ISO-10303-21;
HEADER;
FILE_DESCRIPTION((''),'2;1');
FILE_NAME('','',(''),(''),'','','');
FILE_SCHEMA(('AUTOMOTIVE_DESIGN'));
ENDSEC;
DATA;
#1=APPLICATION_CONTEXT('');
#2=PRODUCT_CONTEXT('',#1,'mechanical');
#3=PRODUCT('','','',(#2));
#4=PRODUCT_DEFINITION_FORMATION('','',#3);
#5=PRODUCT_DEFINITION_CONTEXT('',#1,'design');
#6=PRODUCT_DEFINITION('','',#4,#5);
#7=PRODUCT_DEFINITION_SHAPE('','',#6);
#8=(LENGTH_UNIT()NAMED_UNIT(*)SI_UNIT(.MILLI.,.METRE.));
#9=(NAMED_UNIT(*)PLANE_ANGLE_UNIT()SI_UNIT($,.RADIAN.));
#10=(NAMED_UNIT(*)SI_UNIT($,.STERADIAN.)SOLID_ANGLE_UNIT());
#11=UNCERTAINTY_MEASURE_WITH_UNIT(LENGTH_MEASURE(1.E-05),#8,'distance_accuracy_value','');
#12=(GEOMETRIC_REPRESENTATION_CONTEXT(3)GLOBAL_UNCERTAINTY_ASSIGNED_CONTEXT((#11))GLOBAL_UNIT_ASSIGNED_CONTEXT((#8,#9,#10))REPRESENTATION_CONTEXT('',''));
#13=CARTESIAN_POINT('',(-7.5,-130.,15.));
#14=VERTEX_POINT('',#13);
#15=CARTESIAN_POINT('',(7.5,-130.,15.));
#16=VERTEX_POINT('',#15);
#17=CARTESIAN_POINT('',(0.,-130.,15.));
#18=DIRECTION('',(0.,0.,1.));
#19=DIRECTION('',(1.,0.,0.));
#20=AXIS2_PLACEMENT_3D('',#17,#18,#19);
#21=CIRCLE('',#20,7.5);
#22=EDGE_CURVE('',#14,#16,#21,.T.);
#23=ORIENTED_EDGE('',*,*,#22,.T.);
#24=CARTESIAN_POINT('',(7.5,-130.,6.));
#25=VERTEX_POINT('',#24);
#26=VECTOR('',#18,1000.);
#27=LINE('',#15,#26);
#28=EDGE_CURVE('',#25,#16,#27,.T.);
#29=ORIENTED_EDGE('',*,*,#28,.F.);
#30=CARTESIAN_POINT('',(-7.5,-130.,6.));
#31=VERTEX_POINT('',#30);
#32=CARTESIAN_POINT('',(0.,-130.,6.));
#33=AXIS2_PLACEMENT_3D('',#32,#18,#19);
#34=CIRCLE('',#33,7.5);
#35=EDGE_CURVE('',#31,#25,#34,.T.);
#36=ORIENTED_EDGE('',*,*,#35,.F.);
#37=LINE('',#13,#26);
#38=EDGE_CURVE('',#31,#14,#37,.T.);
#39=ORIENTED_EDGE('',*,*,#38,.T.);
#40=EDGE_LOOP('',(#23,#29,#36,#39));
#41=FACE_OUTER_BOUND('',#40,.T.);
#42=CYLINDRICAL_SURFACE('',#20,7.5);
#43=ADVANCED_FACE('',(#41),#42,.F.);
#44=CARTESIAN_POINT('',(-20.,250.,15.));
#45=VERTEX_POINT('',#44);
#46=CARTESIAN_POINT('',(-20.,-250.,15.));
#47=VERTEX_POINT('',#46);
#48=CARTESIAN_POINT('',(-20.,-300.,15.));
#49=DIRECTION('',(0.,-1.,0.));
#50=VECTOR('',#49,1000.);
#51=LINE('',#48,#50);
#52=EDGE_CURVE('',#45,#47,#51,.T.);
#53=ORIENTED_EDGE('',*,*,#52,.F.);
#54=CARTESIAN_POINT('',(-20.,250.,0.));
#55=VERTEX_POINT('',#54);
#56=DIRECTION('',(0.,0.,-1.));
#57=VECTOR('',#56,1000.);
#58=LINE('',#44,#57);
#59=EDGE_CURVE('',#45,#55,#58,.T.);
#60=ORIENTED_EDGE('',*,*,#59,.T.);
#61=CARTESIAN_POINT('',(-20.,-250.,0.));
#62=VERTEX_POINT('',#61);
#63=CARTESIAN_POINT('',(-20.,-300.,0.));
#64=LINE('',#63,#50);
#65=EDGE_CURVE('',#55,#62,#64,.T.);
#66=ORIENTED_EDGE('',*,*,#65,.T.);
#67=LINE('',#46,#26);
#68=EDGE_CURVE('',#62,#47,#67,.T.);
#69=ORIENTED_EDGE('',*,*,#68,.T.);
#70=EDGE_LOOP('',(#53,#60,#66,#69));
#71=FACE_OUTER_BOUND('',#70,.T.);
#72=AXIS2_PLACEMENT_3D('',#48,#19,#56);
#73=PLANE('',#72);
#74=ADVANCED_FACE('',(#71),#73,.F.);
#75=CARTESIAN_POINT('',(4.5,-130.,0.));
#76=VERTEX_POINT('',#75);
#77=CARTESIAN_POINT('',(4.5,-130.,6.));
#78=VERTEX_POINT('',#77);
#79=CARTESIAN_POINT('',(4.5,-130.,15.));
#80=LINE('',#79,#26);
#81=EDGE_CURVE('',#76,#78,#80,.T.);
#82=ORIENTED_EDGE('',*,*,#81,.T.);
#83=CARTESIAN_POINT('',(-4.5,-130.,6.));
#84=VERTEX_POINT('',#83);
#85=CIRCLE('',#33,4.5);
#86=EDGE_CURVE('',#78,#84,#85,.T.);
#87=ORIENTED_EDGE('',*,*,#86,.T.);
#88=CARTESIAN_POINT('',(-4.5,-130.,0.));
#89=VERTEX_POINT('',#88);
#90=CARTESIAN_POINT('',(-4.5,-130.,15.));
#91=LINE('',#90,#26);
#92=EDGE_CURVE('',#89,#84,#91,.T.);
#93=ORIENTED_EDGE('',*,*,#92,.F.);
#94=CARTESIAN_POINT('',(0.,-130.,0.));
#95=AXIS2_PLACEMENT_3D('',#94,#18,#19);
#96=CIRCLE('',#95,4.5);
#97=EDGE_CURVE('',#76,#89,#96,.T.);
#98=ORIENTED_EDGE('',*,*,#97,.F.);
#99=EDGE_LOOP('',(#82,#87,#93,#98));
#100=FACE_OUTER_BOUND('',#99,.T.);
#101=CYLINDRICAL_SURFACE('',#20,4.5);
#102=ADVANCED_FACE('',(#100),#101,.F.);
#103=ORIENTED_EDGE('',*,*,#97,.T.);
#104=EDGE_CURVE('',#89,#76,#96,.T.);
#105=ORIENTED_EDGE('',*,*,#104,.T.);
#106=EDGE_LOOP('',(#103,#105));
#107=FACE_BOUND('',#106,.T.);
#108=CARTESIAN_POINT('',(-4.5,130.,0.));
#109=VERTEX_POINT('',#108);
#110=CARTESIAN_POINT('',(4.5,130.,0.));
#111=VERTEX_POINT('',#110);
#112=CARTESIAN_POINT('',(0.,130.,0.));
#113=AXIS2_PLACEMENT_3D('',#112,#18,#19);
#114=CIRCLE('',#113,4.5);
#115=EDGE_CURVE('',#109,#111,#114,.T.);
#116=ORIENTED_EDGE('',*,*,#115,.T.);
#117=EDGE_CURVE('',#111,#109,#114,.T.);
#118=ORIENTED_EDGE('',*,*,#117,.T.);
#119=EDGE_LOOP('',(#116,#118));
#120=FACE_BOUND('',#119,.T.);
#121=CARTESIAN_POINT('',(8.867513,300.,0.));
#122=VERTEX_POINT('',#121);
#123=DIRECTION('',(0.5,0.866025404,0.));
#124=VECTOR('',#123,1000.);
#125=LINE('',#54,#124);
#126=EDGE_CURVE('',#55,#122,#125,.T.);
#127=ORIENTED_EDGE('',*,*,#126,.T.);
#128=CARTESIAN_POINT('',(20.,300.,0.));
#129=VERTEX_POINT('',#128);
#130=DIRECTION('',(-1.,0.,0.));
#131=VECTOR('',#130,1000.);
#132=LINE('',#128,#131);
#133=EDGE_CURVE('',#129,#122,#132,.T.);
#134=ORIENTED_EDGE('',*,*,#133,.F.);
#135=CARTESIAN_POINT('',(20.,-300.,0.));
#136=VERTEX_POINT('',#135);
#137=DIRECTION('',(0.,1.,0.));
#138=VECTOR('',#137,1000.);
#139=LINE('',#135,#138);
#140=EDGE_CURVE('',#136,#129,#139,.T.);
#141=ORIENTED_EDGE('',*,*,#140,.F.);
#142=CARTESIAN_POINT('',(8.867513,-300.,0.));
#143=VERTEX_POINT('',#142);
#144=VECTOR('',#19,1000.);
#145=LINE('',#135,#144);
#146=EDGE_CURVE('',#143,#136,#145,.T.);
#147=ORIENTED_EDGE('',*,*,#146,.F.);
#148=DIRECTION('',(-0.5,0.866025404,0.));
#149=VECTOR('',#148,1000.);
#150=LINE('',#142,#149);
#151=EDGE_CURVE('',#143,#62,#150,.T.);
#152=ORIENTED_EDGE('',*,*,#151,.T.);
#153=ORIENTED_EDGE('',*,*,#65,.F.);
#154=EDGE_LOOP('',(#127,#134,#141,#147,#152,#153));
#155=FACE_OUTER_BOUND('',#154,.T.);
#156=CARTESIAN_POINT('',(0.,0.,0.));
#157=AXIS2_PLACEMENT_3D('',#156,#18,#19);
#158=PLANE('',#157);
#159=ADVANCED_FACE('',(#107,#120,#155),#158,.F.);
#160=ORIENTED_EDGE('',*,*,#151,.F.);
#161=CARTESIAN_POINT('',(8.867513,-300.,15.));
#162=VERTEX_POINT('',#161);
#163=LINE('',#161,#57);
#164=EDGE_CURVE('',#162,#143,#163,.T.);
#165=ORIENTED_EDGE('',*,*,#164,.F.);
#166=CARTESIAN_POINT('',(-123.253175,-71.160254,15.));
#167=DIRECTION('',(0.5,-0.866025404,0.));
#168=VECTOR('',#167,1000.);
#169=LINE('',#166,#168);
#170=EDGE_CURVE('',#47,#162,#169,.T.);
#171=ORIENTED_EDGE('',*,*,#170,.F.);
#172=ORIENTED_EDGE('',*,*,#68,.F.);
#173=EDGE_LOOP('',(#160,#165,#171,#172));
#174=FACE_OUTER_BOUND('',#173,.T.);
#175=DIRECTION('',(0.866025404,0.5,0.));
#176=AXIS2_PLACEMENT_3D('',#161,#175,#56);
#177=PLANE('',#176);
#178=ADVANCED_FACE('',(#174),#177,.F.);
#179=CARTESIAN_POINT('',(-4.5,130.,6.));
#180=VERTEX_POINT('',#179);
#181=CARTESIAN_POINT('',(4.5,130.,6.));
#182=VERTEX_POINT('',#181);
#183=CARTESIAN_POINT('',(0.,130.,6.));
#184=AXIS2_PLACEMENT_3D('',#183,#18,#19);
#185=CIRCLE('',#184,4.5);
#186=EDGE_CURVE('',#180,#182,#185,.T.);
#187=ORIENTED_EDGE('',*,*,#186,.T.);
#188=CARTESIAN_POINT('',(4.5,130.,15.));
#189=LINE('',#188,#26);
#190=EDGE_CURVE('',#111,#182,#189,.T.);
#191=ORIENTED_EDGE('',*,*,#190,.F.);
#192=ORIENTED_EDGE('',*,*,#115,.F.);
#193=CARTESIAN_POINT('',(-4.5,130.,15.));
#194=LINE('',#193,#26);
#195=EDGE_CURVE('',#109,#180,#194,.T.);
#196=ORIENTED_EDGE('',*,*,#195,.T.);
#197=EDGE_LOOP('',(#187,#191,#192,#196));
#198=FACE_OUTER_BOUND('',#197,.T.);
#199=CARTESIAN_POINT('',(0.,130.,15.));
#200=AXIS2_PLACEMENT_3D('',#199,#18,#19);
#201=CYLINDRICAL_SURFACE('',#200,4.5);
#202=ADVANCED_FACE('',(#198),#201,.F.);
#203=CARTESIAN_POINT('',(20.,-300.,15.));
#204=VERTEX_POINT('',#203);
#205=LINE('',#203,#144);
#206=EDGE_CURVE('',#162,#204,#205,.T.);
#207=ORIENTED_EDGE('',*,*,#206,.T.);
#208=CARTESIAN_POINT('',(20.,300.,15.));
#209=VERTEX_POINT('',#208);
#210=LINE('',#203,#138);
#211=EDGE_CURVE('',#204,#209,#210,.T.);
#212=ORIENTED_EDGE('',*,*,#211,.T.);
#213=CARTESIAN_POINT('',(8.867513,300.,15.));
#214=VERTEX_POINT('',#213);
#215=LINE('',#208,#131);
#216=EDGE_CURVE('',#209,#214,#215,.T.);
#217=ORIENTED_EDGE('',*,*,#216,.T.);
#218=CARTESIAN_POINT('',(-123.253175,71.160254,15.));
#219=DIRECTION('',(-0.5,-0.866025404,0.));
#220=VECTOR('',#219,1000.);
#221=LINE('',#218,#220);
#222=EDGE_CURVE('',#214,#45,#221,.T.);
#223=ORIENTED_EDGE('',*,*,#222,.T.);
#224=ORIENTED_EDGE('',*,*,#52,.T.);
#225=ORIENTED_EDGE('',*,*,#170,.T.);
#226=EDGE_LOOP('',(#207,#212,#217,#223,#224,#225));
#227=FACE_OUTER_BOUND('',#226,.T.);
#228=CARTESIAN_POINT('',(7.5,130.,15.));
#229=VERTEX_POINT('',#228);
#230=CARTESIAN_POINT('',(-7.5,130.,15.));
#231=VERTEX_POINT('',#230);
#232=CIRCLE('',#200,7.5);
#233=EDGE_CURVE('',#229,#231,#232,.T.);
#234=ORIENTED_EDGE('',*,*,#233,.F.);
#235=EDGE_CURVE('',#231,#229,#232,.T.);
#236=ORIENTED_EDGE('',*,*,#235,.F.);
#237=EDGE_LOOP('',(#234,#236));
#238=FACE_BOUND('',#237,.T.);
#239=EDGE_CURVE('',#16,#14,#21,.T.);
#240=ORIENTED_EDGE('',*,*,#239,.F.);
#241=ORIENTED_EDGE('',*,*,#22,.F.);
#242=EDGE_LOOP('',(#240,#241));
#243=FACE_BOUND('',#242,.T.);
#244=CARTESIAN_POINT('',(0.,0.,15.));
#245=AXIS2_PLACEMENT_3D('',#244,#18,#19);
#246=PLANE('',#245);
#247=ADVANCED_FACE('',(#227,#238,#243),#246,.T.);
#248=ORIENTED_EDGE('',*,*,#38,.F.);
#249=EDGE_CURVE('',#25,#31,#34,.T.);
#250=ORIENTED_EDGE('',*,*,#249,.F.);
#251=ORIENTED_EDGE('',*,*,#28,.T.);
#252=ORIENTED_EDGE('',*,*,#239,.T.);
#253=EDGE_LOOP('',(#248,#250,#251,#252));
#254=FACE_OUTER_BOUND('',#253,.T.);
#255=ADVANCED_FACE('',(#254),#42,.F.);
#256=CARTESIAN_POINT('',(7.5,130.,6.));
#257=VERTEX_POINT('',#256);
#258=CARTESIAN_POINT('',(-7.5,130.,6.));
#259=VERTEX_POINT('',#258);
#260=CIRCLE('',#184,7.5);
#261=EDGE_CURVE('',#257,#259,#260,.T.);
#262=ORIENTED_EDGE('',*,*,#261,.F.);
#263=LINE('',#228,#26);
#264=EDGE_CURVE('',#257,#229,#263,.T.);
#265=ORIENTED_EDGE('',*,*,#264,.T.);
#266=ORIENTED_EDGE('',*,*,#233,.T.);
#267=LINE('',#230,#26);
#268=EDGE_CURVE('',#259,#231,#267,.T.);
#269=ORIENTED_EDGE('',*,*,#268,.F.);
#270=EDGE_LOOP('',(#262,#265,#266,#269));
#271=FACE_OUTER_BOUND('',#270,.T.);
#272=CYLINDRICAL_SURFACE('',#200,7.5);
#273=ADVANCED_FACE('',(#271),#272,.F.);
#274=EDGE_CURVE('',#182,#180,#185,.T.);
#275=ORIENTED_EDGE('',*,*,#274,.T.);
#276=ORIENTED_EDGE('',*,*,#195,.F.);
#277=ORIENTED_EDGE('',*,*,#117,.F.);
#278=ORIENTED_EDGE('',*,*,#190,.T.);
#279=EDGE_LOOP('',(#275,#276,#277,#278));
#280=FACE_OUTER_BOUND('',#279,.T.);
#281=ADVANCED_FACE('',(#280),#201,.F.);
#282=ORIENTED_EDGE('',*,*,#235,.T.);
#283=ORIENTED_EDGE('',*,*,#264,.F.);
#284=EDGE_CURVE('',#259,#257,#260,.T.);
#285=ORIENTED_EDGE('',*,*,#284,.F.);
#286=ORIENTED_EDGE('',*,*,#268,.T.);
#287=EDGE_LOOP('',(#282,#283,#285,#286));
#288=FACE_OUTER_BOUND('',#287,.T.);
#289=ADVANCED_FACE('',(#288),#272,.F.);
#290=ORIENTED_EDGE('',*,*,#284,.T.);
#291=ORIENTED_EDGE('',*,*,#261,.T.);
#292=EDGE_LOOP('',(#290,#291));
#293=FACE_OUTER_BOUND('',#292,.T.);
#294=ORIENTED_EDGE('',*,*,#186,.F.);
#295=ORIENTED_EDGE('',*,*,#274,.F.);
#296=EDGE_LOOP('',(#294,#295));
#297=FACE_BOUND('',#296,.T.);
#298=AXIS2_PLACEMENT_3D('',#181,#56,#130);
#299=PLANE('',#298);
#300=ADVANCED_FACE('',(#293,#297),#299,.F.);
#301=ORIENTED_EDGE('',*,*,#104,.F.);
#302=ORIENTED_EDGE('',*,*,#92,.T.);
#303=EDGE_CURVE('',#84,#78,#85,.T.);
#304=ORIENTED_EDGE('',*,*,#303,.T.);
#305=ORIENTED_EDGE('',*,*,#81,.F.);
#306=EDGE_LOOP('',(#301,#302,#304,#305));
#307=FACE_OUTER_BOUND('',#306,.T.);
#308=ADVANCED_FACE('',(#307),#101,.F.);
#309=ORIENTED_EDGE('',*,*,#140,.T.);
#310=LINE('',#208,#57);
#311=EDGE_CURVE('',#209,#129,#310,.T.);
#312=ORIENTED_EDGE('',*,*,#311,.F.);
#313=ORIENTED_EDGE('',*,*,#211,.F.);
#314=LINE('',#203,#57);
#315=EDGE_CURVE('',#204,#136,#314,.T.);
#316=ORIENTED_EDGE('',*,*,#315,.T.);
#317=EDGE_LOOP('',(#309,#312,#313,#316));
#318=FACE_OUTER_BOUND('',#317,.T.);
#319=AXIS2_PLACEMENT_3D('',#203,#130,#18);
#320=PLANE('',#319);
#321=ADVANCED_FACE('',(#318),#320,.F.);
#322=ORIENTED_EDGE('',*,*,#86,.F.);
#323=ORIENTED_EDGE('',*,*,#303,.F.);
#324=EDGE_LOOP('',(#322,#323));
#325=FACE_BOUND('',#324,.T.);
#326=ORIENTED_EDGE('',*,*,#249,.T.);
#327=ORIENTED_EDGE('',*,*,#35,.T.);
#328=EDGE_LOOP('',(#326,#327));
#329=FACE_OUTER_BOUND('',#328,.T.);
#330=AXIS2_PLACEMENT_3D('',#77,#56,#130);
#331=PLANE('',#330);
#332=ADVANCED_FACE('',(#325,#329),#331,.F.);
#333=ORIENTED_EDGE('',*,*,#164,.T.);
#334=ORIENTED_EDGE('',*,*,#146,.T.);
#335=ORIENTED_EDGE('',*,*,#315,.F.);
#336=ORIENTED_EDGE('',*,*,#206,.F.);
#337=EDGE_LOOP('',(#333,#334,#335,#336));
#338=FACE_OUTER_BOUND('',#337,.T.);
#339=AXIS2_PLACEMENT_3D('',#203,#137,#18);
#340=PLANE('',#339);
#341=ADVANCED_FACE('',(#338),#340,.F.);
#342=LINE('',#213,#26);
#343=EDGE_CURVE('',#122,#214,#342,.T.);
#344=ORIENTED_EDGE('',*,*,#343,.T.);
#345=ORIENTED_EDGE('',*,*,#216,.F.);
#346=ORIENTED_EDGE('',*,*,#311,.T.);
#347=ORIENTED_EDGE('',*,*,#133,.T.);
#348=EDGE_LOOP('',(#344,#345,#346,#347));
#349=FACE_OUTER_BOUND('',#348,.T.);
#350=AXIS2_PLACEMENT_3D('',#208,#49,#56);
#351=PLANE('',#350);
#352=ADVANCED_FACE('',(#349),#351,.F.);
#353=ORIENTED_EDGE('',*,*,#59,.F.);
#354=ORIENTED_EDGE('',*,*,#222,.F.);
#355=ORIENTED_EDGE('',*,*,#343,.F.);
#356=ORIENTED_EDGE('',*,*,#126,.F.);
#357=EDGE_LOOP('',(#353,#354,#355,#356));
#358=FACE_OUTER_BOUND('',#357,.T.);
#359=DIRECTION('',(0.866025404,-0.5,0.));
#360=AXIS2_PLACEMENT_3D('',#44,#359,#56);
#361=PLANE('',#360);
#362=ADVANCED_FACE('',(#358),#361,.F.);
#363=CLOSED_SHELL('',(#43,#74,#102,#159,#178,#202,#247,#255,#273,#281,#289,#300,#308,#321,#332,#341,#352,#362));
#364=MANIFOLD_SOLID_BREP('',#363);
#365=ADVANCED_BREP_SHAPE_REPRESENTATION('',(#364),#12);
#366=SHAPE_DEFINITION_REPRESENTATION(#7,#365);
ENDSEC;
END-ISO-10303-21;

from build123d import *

# Parameters (mm, degrees)
SKETCH_1_W                = 40
SKETCH_1_H                = 600
EXTRUDE_1_DEPTH           = 15
HOLE_WIZARD_1_D           = 9
HOLE_WIZARD_1_CBORE_D     = 15
HOLE_WIZARD_1_CBORE_DEPTH = 9
CHAMFER_1_SIZE            = 50
CHAMFER_1_SIZE2           = 28.867513459


with BuildPart() as part:
    # 草图1 → 凸台-拉伸1 (new body)
    with BuildSketch(Plane.XY):
        Rectangle(SKETCH_1_W, SKETCH_1_H)
    extrude(amount=EXTRUDE_1_DEPTH)

    # 打孔尺寸(%根据)内六角圆柱头螺钉的类型1 (through all)
    with Locations(Plane.XY.offset(15)):
        with Locations((0, -130), (0, 130)):
            CounterBoreHole(HOLE_WIZARD_1_D / 2, HOLE_WIZARD_1_CBORE_D / 2, HOLE_WIZARD_1_CBORE_DEPTH)

    # 倒角1
    chamfer_1_edges = [part.edges().sort_by_distance(p)[0] for p in [
        (-20, 300, 7.5),
        (-20, -300, 7.5),
    ]]
    chamfer_1_side = [part.faces().sort_by_distance(p)[0] for p in [
        (-20, 0, 7.5),
    ]]
    chamfer(chamfer_1_edges, length=CHAMFER_1_SIZE, length2=CHAMFER_1_SIZE2, reference=chamfer_1_side[0])


solid = part.part
